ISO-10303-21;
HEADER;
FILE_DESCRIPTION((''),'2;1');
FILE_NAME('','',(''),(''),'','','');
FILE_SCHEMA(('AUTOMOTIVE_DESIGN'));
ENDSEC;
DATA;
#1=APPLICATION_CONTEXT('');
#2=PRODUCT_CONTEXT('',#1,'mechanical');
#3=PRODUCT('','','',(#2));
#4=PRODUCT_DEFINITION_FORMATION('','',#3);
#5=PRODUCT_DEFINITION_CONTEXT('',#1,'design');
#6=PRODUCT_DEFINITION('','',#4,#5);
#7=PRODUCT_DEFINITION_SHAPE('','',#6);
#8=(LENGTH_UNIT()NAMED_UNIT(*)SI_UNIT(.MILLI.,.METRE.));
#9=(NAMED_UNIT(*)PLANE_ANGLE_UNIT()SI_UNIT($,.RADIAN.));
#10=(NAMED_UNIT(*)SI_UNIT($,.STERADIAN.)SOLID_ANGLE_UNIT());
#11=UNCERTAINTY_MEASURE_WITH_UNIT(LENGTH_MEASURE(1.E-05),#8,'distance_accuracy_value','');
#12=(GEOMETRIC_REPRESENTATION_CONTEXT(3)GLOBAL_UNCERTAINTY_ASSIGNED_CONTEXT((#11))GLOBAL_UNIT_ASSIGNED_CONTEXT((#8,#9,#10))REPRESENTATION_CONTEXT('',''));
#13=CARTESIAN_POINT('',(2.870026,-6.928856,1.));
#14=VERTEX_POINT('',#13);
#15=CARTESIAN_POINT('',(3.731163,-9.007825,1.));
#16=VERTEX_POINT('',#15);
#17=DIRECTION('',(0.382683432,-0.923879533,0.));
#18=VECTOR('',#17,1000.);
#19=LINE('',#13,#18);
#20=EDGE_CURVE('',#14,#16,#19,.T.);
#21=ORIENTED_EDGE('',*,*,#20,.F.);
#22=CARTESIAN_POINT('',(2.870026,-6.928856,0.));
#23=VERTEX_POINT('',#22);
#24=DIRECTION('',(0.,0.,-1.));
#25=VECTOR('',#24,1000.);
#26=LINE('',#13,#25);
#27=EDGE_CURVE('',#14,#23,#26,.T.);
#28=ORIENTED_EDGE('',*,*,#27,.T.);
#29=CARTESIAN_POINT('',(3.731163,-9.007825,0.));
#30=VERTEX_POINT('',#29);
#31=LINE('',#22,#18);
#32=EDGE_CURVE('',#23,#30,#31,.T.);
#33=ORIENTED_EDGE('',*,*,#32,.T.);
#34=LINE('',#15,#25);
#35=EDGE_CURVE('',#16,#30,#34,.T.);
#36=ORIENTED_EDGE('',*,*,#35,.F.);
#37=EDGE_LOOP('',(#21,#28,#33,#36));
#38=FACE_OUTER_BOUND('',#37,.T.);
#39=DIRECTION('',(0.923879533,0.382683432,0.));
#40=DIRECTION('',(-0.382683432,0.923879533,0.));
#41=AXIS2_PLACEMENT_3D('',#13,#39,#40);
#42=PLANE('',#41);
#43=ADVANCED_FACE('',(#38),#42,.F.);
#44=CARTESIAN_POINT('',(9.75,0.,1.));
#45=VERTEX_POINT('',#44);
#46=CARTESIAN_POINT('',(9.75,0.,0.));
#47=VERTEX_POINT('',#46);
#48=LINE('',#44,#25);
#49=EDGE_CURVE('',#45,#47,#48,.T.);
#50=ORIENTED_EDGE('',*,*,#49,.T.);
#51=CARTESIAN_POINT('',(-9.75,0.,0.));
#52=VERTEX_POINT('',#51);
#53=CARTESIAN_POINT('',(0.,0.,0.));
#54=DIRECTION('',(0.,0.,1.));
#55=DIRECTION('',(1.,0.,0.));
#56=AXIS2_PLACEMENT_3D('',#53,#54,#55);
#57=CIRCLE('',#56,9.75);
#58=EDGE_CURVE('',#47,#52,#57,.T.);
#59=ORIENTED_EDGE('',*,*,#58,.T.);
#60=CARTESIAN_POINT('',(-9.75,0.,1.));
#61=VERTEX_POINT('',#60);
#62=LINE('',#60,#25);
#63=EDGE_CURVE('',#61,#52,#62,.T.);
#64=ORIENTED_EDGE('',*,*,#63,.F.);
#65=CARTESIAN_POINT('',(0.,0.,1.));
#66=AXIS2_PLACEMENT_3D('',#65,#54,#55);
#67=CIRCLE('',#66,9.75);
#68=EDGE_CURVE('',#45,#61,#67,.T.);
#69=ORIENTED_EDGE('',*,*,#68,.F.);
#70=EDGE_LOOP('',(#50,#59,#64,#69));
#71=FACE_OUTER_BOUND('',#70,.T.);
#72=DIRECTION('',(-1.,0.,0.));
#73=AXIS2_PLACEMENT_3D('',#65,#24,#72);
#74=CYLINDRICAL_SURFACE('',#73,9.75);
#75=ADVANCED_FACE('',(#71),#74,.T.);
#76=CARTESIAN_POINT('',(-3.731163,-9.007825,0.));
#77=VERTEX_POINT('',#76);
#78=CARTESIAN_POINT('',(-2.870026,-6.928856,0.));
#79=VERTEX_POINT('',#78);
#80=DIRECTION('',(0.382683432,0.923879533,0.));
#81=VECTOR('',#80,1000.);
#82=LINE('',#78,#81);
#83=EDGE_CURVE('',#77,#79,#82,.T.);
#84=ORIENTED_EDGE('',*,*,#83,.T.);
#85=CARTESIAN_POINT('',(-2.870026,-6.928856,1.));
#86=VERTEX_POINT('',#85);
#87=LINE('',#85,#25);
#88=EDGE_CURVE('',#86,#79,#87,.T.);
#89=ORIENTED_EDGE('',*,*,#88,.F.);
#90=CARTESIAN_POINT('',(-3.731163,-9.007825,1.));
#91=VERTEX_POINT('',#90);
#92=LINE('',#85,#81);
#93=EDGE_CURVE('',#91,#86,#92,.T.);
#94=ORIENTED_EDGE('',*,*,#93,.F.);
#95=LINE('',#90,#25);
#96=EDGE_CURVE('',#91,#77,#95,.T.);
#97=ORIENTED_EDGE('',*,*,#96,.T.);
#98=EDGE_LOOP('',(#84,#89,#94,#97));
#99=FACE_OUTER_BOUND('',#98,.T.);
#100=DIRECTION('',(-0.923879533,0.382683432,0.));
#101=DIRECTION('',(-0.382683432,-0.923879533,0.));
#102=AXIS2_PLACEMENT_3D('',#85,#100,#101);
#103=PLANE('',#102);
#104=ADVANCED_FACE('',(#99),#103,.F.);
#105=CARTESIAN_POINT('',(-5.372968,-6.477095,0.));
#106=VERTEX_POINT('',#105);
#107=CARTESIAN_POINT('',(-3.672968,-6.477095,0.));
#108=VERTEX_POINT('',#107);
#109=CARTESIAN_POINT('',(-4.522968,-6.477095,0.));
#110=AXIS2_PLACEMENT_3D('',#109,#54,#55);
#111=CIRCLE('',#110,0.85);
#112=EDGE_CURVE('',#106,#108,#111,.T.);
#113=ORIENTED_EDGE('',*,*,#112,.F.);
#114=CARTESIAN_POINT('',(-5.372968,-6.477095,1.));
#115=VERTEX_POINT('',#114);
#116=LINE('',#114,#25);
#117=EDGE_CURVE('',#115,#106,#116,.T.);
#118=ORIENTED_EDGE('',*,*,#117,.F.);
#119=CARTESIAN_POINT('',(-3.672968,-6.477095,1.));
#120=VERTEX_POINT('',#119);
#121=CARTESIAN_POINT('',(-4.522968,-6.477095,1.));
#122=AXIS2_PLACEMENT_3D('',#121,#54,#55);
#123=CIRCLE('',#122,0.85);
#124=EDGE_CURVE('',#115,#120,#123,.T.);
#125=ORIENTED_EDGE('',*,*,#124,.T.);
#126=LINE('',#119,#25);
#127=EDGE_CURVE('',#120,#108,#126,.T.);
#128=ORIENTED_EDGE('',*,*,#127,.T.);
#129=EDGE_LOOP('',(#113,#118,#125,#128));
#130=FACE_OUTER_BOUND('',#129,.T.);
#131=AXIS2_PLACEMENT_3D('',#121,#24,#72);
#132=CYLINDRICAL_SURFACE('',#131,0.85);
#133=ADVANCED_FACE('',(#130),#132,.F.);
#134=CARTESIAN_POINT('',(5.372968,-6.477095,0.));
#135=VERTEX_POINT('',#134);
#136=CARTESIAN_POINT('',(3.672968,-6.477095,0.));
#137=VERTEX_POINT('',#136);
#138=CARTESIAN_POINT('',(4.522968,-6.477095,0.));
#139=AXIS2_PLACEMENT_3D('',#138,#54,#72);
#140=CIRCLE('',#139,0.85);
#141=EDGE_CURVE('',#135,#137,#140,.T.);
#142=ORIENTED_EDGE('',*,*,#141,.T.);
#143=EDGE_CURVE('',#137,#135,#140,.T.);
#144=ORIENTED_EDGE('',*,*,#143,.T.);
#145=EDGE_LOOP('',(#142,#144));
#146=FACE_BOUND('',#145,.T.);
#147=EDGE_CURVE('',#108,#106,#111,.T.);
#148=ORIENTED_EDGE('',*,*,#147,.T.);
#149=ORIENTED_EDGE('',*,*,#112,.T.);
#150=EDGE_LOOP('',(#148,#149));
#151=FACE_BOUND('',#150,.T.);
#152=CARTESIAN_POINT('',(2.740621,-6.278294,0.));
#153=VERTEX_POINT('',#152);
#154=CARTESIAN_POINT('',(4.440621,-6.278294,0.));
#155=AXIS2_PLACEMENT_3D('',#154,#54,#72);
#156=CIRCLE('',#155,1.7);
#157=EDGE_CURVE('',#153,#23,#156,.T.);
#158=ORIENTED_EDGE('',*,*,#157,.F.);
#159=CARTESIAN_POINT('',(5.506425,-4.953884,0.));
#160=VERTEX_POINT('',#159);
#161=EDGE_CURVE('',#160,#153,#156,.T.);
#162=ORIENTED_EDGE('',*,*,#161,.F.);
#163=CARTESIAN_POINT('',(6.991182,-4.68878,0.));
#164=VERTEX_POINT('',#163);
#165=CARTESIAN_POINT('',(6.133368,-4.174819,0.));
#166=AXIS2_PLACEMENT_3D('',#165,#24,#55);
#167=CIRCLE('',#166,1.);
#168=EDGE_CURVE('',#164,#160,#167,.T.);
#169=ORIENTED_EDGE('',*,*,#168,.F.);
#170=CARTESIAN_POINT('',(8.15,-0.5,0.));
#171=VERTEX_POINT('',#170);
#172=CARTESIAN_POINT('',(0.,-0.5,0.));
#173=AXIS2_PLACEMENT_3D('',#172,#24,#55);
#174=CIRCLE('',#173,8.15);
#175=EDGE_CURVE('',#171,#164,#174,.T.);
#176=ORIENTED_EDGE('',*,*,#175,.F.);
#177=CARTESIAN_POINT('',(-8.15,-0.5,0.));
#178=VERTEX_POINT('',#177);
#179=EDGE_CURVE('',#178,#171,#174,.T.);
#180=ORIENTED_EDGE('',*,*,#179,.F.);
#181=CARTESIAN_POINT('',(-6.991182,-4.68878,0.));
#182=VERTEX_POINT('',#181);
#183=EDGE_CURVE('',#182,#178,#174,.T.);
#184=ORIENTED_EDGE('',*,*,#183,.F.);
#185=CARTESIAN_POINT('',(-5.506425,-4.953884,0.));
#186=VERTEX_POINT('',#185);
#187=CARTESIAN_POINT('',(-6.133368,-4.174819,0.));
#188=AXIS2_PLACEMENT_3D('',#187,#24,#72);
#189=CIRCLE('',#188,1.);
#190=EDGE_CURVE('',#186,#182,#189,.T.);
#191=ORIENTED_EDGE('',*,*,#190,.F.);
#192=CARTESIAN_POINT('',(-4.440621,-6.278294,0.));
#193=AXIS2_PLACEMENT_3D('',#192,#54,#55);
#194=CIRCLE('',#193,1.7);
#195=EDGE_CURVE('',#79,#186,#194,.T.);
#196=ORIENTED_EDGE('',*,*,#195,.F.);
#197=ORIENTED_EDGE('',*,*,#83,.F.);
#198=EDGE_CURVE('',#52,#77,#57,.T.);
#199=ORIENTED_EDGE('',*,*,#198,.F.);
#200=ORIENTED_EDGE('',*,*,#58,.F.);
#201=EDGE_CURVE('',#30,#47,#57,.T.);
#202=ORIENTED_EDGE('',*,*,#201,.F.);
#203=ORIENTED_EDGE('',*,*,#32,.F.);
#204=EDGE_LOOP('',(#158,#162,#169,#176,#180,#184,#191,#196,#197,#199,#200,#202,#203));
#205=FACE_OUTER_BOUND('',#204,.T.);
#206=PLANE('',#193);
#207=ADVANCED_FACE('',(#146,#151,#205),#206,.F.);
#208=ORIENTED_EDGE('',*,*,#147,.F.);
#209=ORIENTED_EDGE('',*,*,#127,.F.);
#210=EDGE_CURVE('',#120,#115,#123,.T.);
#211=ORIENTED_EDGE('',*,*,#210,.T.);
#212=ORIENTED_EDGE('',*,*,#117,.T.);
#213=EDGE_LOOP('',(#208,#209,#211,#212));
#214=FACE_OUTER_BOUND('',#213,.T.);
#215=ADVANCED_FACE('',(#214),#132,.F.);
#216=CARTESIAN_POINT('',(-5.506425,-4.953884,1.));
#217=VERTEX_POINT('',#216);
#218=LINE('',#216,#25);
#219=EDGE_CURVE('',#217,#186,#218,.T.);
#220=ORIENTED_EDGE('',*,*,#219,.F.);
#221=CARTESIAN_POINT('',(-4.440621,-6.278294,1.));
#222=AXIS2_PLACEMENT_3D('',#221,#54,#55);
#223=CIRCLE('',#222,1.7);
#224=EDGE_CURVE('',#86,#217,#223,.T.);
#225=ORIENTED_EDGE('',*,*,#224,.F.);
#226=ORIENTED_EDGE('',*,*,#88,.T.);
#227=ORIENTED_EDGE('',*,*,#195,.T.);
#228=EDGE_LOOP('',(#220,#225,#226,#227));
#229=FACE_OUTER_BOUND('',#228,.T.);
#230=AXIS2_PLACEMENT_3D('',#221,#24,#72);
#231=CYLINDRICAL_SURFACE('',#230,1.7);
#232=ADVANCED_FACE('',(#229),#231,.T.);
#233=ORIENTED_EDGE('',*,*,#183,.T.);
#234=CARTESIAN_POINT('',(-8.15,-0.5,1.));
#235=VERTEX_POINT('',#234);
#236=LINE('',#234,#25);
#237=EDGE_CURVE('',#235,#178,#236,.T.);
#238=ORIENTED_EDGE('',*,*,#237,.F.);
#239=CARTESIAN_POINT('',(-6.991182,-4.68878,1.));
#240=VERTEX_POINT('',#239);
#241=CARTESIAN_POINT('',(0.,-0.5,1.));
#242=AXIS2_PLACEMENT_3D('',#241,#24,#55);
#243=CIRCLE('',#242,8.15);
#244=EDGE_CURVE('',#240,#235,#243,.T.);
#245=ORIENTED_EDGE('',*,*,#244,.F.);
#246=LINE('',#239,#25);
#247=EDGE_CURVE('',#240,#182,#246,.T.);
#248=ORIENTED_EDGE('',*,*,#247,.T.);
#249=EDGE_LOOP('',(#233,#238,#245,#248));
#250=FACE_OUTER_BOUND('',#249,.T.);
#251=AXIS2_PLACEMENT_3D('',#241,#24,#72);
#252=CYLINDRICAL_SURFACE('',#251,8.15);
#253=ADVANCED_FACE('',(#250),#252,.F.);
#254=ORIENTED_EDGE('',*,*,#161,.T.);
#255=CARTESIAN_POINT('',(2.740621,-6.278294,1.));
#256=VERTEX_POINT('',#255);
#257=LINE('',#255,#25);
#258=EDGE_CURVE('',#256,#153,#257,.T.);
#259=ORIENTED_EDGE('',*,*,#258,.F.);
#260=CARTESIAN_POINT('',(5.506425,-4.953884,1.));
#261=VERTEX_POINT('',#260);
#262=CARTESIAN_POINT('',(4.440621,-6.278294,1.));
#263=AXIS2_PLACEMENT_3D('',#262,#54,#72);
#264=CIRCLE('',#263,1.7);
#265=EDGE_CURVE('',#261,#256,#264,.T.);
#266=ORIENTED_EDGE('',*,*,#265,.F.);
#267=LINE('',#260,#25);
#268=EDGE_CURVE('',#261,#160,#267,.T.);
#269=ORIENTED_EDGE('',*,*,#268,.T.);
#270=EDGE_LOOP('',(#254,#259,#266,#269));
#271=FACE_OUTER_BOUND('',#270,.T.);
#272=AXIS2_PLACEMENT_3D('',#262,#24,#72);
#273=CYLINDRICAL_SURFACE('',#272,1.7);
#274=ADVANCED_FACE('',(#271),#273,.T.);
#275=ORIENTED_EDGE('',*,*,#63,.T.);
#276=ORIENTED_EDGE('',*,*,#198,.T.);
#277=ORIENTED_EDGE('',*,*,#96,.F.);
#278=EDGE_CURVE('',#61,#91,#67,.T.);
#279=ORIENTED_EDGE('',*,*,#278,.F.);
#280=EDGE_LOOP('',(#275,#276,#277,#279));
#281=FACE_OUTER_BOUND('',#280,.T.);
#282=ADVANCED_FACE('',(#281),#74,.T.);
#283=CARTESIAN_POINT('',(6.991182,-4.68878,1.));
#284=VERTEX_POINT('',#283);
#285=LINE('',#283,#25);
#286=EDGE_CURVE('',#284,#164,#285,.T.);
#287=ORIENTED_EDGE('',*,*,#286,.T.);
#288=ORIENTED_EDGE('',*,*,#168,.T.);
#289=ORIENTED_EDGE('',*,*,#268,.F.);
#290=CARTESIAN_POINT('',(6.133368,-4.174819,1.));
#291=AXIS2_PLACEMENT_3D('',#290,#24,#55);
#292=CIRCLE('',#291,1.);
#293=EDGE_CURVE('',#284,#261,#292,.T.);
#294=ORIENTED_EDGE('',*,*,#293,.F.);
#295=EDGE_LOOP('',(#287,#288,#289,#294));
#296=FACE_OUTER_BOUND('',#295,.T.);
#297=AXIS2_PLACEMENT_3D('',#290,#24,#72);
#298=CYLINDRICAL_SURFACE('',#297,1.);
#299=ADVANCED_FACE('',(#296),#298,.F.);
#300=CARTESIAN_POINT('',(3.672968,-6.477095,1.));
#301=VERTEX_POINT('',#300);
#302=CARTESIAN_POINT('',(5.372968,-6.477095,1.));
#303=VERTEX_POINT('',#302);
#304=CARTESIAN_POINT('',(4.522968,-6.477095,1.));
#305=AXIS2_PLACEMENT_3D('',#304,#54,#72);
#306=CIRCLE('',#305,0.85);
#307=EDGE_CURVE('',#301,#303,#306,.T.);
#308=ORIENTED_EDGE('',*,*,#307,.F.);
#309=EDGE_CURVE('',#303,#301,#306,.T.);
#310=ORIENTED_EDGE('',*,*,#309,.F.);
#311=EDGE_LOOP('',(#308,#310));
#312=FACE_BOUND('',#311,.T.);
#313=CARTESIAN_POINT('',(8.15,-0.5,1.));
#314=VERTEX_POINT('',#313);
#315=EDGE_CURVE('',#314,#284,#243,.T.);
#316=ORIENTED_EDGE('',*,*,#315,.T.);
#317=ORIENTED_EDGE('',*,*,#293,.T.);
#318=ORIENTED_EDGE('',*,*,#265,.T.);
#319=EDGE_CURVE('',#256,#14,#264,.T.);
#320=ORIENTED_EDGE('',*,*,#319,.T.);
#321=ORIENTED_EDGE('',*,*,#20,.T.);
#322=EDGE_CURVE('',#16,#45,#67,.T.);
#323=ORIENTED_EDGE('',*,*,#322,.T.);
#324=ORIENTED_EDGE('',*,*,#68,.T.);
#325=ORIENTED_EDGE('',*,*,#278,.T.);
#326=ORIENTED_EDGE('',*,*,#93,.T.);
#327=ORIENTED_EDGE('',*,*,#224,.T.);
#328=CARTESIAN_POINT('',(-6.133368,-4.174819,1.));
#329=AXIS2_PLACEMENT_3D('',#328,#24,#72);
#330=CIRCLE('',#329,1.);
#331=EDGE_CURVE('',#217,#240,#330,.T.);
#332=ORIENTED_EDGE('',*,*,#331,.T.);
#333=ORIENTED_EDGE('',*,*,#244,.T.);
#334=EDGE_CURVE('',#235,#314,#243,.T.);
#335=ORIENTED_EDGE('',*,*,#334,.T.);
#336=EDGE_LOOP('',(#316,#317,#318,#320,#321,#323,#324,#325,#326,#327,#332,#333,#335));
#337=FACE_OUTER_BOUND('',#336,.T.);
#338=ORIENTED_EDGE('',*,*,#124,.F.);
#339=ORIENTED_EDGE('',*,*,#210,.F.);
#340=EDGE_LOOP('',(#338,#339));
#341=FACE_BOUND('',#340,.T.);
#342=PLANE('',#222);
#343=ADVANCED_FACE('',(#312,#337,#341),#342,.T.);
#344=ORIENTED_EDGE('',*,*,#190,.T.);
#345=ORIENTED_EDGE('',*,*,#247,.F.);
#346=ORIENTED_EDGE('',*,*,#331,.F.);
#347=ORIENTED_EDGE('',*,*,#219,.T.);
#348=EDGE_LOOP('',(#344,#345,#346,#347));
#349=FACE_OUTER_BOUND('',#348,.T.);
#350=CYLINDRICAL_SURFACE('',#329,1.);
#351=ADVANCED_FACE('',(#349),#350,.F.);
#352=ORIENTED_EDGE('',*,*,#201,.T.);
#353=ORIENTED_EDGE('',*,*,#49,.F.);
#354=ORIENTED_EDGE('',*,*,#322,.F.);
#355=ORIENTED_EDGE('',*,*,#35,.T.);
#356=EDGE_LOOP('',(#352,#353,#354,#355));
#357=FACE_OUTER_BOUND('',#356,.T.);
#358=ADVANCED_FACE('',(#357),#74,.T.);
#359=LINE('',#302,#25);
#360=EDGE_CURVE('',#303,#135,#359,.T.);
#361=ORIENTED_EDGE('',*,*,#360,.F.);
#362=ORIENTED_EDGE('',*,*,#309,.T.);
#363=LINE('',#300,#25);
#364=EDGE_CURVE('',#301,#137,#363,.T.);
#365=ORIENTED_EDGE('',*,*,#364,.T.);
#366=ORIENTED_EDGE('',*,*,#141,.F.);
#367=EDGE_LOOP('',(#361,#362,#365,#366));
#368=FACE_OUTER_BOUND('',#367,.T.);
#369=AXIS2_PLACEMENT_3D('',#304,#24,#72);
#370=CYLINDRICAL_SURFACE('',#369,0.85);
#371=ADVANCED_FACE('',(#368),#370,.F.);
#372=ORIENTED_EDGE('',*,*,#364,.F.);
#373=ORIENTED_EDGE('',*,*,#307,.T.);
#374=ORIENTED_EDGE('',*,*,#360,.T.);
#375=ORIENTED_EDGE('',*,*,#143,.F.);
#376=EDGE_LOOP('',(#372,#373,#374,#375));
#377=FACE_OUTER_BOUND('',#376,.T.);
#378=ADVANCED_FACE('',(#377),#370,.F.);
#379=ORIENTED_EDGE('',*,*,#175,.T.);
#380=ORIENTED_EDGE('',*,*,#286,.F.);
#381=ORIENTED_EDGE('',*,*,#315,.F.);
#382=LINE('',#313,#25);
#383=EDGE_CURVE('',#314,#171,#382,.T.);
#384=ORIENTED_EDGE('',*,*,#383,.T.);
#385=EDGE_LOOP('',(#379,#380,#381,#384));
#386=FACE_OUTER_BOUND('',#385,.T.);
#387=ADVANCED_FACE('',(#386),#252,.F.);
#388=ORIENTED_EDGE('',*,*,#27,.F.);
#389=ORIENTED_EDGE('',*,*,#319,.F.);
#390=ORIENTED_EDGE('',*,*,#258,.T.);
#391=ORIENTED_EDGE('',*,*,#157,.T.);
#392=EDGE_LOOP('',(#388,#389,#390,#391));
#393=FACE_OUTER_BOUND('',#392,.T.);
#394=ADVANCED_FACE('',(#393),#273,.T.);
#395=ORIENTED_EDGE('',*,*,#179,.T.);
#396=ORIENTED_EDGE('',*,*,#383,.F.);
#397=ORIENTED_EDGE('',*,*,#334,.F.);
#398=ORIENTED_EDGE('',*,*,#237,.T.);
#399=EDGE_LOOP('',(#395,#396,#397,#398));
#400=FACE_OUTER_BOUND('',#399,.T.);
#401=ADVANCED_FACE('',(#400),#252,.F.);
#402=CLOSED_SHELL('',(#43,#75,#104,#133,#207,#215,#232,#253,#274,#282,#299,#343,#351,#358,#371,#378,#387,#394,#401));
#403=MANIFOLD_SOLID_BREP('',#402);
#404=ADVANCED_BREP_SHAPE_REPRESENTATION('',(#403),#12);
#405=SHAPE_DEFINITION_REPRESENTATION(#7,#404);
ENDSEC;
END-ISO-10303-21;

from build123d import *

# Parameters (mm, degrees)
SKETCH_1_R        = 0.85
EXTRUDE_967_DEPTH = 1


with BuildPart() as part:
    # 草图1 → Extrude 967 (new body)
    with BuildSketch(Plane.XY):
        with BuildLine():
            Line((-2.870026243, -6.928856281), (-3.731163466, -9.007825442))
            ThreePointArc((-3.731163466, -9.007825442), (0, 9.75), (3.731163466, -9.007825442))
            Line((3.731163466, -9.007825442), (2.870026243, -6.928856281))
            ThreePointArc((2.870026243, -6.928856281), (3.421390109, -4.91771829), (5.506424922, -4.953884028))
            ThreePointArc((5.506424922, -4.953884028), (6.309138908, -5.1592502), (6.991181868, -4.688779786))
            ThreePointArc((6.991181868, -4.688779786), (0, 7.65), (-6.991181868, -4.688779786))
            ThreePointArc((-6.991181868, -4.688779786), (-6.309138908, -5.1592502), (-5.506424922, -4.953884028))
            ThreePointArc((-5.506424922, -4.953884028), (-3.421390109, -4.91771829), (-2.870026243, -6.928856281))
        make_face()
        with Locations((-4.522967504, -6.47709541)):
            Circle(SKETCH_1_R, mode=Mode.SUBTRACT)
        with Locations(Location((4.522967504, -6.47709541, 0), (0, 0, 180))):
            Circle(SKETCH_1_R, mode=Mode.SUBTRACT)
    extrude(amount=EXTRUDE_967_DEPTH)


solid = part.part
